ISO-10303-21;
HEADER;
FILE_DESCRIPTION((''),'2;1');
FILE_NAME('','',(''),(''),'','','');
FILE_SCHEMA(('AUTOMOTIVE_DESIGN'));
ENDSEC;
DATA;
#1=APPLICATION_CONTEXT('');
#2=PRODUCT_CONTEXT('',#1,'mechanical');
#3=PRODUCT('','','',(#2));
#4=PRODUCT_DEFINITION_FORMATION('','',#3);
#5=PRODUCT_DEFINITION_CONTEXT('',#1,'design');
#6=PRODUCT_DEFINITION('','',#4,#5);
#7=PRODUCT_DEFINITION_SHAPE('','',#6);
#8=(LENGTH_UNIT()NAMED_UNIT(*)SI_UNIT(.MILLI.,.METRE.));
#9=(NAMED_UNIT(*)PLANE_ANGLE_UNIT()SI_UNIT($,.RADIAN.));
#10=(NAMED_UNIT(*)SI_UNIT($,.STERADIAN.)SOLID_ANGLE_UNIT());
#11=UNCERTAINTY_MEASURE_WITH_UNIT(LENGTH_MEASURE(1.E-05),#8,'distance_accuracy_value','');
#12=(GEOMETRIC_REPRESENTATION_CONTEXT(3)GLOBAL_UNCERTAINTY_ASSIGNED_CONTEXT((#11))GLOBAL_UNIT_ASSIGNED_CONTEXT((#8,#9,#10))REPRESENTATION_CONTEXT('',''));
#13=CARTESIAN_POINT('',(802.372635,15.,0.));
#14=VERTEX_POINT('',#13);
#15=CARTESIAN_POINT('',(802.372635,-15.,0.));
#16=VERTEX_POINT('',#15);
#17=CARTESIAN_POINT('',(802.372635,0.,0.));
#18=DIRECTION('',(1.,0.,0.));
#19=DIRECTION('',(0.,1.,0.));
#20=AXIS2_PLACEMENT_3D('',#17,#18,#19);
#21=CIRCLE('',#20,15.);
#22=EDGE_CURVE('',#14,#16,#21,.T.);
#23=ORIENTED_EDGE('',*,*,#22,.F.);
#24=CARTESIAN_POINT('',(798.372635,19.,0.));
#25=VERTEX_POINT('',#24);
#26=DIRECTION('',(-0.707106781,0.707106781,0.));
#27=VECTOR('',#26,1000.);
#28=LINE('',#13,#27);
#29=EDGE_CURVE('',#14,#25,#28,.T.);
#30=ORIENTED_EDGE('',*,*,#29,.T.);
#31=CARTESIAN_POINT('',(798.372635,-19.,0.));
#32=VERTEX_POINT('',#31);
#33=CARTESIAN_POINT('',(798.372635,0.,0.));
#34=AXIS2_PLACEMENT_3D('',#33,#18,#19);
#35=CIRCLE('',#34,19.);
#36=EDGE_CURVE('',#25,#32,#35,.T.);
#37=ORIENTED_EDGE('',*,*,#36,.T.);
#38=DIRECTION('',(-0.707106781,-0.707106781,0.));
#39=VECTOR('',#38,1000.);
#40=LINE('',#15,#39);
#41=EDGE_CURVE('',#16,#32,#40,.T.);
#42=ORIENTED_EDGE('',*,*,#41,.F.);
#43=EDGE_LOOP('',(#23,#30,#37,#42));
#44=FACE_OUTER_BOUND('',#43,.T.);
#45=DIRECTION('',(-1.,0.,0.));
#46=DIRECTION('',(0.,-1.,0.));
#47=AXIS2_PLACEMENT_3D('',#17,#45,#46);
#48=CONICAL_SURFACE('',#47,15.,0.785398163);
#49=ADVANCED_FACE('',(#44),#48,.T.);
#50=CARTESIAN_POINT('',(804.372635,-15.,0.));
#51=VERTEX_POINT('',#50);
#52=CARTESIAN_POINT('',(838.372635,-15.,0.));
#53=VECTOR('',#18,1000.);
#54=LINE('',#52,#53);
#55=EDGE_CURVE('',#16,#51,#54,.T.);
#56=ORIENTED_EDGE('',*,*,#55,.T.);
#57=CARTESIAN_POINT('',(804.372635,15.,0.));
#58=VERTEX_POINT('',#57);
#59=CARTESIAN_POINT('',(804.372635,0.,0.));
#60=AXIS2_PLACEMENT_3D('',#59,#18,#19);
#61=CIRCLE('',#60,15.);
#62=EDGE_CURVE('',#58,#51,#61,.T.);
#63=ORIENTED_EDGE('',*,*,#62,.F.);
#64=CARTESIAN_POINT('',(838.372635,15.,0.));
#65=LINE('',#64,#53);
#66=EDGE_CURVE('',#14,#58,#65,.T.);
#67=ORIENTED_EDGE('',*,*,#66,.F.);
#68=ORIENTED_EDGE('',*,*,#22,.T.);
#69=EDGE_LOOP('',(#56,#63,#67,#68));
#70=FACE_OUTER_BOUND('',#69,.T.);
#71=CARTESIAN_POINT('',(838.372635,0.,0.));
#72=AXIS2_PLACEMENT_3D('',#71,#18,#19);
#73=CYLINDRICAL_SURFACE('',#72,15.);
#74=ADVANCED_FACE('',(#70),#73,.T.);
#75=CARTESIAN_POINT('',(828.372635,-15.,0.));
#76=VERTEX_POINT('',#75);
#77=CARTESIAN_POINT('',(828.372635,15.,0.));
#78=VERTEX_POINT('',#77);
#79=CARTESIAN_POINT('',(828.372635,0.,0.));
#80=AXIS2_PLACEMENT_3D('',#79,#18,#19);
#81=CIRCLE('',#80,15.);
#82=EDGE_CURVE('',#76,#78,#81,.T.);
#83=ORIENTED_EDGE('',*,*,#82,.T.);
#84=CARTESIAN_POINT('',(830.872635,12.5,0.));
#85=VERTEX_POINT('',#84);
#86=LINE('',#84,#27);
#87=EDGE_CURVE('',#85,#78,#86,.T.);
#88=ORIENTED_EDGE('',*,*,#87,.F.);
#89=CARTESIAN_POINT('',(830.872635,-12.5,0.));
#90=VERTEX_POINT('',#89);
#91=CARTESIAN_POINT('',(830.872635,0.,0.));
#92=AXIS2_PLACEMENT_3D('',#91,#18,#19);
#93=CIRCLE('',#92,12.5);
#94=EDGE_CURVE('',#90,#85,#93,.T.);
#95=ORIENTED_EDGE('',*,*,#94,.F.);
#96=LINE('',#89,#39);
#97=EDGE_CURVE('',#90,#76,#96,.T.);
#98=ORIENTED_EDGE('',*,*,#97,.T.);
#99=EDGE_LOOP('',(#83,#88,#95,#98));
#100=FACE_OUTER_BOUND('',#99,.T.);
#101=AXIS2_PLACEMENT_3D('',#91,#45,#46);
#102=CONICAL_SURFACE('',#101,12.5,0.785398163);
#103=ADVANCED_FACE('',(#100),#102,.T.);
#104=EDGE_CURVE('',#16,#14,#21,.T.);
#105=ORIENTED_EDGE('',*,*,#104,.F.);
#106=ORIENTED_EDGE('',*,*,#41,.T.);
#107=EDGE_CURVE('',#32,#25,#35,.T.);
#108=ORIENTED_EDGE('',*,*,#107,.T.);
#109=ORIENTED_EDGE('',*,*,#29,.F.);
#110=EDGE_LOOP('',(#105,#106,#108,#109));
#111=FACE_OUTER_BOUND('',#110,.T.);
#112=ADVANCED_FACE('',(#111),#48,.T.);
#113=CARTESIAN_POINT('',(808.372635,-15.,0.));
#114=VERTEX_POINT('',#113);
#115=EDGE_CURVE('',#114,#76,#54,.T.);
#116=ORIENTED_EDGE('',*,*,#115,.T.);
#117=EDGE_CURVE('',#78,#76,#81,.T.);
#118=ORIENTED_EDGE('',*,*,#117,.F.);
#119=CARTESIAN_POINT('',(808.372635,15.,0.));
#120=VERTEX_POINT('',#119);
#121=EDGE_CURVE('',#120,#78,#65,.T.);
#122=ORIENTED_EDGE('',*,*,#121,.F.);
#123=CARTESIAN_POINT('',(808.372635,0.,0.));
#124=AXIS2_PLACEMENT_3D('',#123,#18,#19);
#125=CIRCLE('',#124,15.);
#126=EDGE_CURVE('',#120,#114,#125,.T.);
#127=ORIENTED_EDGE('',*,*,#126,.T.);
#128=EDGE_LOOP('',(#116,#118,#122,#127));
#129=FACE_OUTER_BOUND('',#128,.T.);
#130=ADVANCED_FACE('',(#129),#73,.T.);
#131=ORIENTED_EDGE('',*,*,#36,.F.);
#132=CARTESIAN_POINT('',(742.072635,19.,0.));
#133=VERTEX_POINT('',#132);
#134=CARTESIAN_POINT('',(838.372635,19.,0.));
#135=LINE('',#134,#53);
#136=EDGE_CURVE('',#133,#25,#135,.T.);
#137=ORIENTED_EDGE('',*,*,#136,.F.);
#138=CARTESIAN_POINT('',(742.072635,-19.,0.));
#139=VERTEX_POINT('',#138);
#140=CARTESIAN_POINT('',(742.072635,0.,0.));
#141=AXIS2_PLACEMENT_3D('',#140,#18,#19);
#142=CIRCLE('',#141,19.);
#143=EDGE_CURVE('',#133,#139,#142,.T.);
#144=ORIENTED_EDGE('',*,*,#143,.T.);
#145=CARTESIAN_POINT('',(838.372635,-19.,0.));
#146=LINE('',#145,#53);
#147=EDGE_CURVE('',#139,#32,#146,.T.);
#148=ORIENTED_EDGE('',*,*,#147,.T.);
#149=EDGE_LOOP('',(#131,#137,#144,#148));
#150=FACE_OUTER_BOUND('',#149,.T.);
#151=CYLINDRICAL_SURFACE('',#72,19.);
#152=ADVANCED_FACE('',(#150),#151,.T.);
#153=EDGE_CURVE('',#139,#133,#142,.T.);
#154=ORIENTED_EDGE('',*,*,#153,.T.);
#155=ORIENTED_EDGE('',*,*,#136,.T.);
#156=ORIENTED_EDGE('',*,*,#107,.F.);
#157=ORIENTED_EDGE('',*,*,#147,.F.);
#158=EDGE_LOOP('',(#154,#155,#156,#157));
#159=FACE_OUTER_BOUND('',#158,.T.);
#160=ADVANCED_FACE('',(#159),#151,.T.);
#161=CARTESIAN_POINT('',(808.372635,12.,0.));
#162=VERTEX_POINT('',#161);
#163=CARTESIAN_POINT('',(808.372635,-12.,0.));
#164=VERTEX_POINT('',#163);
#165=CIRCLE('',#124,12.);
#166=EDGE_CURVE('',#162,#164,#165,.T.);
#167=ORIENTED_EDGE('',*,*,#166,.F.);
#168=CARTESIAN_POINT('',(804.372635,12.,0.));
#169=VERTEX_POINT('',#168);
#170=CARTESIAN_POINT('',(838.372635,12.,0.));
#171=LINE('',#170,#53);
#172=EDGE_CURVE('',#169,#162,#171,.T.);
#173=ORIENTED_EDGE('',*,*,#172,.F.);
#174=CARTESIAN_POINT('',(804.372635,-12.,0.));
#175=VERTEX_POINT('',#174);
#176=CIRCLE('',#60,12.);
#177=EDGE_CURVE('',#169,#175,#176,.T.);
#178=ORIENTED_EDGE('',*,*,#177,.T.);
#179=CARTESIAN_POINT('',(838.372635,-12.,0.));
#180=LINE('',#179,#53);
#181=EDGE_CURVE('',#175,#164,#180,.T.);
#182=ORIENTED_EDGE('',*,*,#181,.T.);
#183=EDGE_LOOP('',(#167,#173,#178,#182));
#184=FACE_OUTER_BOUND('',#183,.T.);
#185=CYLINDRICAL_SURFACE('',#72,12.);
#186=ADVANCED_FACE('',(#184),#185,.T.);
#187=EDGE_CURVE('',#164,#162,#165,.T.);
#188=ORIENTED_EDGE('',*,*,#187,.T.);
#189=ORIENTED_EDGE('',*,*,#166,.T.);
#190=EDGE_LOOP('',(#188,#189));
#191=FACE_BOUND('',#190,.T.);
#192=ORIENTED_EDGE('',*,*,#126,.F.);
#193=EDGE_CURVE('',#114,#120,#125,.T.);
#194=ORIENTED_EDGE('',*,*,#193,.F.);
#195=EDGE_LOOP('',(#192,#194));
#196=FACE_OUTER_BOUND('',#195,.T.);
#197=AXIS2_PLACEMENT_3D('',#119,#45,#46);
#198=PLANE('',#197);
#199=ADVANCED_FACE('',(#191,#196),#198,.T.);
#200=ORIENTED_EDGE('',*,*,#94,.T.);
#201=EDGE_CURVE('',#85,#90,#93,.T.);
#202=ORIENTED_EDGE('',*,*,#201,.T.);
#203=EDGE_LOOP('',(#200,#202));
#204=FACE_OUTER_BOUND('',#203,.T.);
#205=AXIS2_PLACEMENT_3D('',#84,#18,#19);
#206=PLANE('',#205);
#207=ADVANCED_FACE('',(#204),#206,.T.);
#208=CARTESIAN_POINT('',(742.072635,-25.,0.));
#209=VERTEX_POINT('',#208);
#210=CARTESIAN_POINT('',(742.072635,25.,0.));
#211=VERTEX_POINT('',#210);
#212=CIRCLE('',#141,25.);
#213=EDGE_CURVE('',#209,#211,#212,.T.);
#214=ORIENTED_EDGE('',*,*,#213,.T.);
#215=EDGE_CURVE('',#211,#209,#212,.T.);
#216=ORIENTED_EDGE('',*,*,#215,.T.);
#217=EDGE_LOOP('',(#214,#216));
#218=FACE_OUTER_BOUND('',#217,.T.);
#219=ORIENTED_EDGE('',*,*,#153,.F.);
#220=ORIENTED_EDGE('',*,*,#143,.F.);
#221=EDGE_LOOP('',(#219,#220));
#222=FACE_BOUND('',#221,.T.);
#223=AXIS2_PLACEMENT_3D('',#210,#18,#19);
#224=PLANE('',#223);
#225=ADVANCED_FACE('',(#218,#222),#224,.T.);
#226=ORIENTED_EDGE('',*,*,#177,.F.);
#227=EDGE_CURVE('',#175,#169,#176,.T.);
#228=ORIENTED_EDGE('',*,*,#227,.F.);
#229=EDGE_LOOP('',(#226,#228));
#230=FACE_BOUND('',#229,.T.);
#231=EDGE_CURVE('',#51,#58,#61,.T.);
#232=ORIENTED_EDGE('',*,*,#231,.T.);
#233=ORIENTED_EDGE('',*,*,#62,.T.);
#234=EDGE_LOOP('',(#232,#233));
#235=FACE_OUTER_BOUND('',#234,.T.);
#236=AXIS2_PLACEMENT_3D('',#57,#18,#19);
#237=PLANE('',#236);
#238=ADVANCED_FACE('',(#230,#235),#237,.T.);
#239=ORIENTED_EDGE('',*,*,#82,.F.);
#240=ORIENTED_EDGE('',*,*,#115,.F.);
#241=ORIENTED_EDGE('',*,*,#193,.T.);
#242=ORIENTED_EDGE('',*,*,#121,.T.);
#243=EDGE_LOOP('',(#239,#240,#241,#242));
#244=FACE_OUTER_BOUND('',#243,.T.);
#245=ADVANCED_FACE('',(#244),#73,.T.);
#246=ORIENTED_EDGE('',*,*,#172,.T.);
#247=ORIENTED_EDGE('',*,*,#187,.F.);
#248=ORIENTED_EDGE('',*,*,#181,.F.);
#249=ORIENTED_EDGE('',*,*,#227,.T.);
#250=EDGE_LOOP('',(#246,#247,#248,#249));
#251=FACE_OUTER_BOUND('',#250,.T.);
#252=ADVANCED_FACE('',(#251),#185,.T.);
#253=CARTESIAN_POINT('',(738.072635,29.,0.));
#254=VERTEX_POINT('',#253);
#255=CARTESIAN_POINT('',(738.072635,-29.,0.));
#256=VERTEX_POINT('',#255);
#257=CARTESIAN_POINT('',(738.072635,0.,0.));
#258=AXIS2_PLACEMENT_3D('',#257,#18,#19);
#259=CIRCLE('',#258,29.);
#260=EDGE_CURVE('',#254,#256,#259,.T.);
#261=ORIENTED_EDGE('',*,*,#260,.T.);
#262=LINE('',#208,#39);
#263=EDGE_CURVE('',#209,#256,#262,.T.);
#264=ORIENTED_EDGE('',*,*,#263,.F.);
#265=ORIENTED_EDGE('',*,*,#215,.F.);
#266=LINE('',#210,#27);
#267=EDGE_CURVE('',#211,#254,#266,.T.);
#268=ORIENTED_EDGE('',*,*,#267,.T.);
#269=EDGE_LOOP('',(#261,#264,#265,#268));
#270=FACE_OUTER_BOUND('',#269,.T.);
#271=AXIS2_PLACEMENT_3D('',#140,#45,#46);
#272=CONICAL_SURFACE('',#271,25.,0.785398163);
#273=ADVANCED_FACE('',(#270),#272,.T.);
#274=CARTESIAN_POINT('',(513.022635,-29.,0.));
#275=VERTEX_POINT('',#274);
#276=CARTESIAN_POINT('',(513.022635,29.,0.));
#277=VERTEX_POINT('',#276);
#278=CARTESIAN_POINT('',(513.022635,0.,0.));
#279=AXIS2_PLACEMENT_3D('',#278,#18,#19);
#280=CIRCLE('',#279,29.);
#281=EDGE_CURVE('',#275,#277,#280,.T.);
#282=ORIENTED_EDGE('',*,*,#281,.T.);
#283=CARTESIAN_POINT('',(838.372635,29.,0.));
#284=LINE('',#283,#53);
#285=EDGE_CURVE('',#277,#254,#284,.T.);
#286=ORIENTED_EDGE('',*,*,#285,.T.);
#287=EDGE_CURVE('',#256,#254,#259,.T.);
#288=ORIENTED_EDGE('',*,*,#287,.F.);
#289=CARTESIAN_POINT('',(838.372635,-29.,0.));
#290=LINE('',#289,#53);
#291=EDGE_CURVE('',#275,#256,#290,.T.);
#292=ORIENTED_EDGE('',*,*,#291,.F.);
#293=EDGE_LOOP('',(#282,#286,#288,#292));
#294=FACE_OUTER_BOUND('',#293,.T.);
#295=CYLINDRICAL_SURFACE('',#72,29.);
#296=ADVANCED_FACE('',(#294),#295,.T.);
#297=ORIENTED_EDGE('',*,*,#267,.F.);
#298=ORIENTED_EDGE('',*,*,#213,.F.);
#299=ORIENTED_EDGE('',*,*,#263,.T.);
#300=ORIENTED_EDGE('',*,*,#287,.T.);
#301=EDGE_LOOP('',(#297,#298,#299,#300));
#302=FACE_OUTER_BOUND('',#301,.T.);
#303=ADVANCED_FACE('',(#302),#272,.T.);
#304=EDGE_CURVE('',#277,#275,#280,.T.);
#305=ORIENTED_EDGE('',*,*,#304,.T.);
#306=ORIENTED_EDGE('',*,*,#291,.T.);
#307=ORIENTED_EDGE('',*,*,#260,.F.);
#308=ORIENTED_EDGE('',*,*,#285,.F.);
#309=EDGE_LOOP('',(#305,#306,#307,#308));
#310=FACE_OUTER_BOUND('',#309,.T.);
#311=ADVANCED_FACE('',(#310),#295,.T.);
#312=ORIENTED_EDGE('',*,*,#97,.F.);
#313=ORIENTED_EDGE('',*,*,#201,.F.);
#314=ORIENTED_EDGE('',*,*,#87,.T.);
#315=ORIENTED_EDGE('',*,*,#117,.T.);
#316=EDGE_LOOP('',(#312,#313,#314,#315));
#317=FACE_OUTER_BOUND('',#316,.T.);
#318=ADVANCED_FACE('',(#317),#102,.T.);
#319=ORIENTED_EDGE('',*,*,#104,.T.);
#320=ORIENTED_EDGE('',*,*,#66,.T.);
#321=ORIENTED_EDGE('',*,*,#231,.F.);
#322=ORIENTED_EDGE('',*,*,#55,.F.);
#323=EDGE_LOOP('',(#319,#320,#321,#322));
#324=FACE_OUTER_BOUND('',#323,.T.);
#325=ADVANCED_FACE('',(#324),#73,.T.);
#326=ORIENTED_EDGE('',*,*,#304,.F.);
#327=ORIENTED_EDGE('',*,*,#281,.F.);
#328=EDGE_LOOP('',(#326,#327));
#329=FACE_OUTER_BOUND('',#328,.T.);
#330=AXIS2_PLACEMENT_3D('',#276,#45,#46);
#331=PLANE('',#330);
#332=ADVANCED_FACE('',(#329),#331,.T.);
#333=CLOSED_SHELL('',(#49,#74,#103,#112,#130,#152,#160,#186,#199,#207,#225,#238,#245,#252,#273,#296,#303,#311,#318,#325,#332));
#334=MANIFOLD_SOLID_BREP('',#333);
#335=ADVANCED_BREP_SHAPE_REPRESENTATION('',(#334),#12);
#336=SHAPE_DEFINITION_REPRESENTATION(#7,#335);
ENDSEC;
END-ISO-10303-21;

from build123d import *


with BuildPart() as part:
    # Sketch1 → Revolve1 (revolve)
    with BuildSketch(Plane.XY):
        Polygon((828.372635386, 15), (808.372635386, 15), (808.372635386, 12), (804.372635386, 12), (804.372635386, 15), (802.372635386, 15), (798.372635386, 19), (742.072635386, 19), (742.072635386, 25), (738.072635386, 29), (684.582635386, 29), (666.582635386, 29), (513.022635386, 29), (513.022635386, 0), (830.872635386, 0), (830.872635386, 12.5), align=None)
    revolve(axis=Axis((838.372635386, 0, 0), (-1, 0, 0)))


solid = part.part
